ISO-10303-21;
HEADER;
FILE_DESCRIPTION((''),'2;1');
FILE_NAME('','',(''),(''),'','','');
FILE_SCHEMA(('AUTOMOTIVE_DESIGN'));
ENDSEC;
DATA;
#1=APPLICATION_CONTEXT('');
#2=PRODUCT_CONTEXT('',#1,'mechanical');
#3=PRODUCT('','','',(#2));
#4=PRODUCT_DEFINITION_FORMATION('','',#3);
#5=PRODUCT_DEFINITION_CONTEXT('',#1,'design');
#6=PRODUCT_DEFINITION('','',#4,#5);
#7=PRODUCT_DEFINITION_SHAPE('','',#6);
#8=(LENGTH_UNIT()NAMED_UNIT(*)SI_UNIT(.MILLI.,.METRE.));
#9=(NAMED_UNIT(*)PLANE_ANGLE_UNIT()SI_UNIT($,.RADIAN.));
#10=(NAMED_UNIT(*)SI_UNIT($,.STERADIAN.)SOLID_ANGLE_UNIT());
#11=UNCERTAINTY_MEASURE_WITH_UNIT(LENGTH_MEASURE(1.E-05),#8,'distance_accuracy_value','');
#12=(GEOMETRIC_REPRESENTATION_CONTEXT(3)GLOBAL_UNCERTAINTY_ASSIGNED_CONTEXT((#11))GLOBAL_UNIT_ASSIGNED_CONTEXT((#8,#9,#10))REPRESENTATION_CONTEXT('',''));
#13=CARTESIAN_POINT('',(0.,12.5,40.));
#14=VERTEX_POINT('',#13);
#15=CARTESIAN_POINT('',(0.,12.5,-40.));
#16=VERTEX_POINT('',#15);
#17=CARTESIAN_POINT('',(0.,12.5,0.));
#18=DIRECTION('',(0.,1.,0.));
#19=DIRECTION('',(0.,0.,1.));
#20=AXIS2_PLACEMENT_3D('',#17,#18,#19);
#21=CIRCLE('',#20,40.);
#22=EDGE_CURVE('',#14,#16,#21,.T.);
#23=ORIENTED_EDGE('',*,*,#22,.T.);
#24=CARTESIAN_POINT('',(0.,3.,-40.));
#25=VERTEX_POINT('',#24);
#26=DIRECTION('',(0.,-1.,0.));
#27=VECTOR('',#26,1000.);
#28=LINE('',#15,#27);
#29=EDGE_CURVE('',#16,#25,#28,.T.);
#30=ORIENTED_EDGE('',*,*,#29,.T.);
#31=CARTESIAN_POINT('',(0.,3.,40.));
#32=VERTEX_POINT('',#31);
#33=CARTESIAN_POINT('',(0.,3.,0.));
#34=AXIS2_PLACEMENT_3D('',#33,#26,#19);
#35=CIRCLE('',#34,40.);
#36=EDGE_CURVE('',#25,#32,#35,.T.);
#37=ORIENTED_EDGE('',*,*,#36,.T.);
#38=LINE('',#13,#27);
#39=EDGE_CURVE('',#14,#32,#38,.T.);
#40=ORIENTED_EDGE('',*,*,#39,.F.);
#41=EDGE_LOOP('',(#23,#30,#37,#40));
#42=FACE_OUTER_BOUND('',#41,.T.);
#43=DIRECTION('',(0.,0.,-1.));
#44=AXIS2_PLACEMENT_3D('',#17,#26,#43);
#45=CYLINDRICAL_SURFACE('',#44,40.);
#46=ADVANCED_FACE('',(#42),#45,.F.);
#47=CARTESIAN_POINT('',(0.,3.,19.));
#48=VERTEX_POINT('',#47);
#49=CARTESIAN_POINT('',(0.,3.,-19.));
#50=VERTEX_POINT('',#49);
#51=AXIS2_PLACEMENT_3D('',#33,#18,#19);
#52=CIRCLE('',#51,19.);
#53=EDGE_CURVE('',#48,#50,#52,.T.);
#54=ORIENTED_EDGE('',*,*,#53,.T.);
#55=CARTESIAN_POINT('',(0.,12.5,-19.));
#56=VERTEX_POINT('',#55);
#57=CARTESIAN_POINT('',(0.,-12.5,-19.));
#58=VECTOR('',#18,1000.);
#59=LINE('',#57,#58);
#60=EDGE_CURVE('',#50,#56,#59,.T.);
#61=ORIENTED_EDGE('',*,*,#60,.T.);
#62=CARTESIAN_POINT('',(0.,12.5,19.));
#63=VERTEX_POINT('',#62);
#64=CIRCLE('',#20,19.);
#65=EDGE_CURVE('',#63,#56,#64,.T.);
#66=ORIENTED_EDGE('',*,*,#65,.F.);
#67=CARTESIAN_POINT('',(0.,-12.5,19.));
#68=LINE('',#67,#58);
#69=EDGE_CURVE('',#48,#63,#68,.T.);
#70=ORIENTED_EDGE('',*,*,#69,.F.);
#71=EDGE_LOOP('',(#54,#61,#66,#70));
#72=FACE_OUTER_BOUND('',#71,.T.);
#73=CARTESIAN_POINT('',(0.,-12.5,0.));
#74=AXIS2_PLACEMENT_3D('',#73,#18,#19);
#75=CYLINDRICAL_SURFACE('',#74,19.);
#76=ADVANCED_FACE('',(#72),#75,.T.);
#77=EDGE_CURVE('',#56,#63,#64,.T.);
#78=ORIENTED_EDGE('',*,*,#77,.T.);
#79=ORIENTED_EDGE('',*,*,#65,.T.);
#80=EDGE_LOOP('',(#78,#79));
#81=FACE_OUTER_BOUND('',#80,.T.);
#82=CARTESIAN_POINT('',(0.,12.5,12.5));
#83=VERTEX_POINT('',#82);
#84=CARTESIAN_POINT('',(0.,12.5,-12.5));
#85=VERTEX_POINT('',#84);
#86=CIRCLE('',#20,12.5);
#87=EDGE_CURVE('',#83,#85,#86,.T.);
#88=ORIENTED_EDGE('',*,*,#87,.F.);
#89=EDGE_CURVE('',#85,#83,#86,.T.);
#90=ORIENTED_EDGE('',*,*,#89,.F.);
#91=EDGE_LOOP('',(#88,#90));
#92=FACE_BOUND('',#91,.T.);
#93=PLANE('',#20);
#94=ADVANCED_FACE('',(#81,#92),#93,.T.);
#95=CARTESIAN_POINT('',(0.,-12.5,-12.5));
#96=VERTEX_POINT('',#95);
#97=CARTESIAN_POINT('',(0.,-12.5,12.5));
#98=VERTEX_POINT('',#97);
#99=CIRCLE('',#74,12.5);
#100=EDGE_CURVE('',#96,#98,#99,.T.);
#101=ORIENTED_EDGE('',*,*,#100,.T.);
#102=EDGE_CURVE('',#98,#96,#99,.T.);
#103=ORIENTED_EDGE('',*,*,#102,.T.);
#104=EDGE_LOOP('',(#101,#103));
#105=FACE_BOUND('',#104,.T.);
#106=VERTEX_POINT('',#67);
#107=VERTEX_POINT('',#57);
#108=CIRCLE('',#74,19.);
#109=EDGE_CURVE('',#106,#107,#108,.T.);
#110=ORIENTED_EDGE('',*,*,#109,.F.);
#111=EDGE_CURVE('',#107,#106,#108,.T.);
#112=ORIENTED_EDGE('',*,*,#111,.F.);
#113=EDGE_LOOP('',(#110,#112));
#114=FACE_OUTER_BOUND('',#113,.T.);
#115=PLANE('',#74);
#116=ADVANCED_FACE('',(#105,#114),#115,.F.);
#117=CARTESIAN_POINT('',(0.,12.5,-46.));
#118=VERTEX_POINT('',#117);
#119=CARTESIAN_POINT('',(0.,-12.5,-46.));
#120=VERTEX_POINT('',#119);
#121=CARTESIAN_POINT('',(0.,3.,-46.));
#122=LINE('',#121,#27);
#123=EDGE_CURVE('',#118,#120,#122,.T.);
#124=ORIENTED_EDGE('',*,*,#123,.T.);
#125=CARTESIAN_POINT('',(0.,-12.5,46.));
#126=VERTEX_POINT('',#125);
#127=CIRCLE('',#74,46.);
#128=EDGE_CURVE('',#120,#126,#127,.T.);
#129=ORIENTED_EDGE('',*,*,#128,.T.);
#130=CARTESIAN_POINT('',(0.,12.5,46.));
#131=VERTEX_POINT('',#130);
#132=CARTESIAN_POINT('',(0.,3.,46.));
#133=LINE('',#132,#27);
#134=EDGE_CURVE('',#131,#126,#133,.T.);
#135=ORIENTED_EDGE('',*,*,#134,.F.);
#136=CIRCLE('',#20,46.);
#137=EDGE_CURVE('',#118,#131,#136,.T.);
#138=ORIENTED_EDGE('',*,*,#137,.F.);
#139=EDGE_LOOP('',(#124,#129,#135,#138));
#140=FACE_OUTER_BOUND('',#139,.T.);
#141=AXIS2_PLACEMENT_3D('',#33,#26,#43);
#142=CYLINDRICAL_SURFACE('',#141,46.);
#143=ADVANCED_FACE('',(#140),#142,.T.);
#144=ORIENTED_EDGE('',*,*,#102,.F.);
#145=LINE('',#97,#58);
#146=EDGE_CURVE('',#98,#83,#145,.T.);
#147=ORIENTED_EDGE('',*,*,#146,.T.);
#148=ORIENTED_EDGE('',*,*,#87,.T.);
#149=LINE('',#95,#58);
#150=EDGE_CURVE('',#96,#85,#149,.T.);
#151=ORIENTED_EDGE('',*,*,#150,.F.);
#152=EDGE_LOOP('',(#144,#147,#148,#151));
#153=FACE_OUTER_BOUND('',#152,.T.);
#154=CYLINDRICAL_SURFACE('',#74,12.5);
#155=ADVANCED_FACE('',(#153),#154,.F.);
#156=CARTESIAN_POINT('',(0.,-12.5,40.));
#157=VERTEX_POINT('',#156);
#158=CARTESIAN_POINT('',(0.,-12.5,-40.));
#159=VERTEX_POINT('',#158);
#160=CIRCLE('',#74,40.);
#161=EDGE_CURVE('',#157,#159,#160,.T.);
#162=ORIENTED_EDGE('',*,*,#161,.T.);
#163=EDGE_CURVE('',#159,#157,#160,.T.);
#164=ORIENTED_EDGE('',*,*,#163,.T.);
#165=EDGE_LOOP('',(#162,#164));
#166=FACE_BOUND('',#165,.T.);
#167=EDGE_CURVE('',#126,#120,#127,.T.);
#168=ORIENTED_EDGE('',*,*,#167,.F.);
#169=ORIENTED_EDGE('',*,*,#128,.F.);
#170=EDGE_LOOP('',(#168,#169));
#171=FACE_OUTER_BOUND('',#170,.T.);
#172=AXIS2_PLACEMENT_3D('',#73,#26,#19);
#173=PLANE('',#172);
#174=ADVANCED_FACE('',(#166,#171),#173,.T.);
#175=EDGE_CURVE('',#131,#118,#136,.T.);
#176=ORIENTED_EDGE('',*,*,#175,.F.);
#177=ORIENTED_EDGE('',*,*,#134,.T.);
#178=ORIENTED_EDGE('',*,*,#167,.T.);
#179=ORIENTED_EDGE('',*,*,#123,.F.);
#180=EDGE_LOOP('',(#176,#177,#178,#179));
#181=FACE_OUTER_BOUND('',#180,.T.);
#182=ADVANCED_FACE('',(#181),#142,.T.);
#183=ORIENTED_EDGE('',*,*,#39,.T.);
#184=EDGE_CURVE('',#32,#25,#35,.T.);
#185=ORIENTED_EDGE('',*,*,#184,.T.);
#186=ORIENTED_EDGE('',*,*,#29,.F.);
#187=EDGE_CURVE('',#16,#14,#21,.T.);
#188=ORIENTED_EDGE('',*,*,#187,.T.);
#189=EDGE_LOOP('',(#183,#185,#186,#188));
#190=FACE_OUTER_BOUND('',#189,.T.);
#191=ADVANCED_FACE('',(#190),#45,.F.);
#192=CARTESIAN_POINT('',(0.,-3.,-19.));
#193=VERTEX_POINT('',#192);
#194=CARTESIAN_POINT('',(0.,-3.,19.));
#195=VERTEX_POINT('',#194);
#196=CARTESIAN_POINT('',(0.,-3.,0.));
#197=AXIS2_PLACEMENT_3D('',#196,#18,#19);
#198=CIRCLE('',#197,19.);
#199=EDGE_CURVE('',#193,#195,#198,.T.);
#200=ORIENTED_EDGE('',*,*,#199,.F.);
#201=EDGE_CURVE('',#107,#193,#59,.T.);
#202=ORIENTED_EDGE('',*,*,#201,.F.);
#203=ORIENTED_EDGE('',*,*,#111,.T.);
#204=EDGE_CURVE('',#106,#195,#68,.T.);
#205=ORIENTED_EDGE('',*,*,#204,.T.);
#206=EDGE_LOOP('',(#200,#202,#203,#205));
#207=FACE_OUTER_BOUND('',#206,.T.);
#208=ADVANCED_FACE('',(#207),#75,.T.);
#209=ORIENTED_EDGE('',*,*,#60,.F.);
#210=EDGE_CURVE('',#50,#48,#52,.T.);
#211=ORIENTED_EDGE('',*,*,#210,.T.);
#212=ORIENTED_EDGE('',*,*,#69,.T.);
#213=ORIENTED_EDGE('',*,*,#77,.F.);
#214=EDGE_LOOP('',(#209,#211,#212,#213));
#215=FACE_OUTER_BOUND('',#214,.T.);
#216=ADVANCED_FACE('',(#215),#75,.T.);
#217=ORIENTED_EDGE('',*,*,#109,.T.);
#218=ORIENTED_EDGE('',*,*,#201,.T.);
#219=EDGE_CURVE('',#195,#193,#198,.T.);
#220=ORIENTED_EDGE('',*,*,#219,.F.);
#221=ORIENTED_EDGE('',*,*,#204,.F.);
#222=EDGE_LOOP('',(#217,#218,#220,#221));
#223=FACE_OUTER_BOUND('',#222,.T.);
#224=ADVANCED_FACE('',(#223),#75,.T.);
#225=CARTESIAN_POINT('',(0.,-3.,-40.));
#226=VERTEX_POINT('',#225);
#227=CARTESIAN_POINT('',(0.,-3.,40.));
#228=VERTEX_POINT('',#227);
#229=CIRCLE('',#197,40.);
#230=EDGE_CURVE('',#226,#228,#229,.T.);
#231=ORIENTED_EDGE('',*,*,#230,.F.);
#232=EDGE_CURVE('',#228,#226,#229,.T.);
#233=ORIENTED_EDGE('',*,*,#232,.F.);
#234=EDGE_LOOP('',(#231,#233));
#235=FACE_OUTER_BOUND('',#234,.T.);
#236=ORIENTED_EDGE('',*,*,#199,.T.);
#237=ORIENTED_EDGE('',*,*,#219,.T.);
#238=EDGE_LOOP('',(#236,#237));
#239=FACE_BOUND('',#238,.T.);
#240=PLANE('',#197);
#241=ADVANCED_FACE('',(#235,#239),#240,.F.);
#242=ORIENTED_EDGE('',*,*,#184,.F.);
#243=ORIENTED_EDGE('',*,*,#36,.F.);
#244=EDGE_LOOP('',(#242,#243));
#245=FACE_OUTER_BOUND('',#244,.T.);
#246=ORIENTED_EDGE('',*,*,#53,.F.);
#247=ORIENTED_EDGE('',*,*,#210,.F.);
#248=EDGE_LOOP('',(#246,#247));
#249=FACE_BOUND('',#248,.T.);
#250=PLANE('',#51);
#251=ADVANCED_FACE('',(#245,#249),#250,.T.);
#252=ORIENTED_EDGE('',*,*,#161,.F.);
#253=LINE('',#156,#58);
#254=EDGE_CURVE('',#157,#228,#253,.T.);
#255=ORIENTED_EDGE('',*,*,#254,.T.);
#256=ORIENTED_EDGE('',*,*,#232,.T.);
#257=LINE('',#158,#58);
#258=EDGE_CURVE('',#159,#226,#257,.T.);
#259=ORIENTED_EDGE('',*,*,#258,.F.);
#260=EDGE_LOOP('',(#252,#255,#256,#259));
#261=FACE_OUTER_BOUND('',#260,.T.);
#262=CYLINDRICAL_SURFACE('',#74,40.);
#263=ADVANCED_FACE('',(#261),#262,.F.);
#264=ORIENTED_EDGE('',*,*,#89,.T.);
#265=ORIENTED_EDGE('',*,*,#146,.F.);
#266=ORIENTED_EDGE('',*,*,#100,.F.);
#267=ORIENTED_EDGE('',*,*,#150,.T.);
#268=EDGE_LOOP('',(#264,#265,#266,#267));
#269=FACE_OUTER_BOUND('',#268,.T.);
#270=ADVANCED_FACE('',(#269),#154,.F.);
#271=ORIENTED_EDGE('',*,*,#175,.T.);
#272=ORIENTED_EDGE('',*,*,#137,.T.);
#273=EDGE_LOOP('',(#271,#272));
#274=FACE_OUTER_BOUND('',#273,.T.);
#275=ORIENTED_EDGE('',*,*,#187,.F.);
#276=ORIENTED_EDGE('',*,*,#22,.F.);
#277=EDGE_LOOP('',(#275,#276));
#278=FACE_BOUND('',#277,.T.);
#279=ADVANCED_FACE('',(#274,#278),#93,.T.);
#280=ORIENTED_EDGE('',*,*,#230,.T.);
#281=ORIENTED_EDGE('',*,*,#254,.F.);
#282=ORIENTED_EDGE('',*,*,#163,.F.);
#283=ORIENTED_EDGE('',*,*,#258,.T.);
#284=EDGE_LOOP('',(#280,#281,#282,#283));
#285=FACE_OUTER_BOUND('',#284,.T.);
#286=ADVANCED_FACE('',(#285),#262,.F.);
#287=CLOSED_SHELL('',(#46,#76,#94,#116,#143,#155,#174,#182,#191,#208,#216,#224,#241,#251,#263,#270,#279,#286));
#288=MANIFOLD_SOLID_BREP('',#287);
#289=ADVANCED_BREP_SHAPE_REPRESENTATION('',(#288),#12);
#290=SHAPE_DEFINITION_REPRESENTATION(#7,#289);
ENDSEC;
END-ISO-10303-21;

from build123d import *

# Parameters (mm, degrees)
BASE_DISC_SKETCH_R = 46
BASE_DISC_92_DEPTH = 3
RIM_START          = 9.5
RIM_SKETCH_R       = 46
RIM_SKETCH_R_2     = 40
RIM_92X_80_DEPTH   = 9.5
HUB_SKETCH_R       = 19
HUB_SKETCH_R_2     = 12.5
HUB_38_DEPTH       = 25
BORE_SKETCH_R      = 12.5
BORE_25_DEPTH      = 25


with BuildPart() as part:
    # Base Disc Sketch → Base Disc Ø92 (new, symmetric)
    with BuildSketch(Plane(origin=(0, 0, 0), x_dir=(1, 0, 0), z_dir=(0, 1, 0))):
        with Locations(Location((0, 0, 0), (0, 0, 270))):
            Circle(BASE_DISC_SKETCH_R)
    extrude(amount=BASE_DISC_92_DEPTH, both=True)

    # Rim Sketch → Rim Ø92xØ80 (add)
    with BuildSketch(Plane(origin=(0, 3, 0), x_dir=(1, 0, 0), z_dir=(0, 1, 0)).offset(RIM_START)):
        with Locations(Location((0, 0, 0), (0, 0, 270))):
            Circle(RIM_SKETCH_R)
        with Locations(Location((0, 0, 0), (0, 0, 270))):
            Circle(RIM_SKETCH_R_2, mode=Mode.SUBTRACT)
    rim_92x_80 = extrude(amount=-RIM_92X_80_DEPTH)

    # Rim Mirror: Rim Ø92xØ80 across plane
    add(rim_92x_80.mirror(Plane.ZX))

    # Hub Sketch → Hub Ø38 (add)
    with BuildSketch(Plane(origin=(0, 12.5, 0), x_dir=(1, 0, 0), z_dir=(0, 1, 0))):
        with Locations(Location((0, 0, 0), (0, 0, 270))):
            Circle(HUB_SKETCH_R)
        with Locations(Location((0, 0, 0), (0, 0, 270))):
            Circle(HUB_SKETCH_R_2, mode=Mode.SUBTRACT)
    extrude(amount=-HUB_38_DEPTH)

    # Bore Sketch → Bore Ø25 (cut)
    with BuildSketch(Plane(origin=(0, 3, 0), x_dir=(1, 0, 0), z_dir=(0, 1, 0))):
        with Locations(Location((0, 0, 0), (0, 0, 270))):
            Circle(BORE_SKETCH_R)
    extrude(amount=-BORE_25_DEPTH, mode=Mode.SUBTRACT)


solid = part.part
